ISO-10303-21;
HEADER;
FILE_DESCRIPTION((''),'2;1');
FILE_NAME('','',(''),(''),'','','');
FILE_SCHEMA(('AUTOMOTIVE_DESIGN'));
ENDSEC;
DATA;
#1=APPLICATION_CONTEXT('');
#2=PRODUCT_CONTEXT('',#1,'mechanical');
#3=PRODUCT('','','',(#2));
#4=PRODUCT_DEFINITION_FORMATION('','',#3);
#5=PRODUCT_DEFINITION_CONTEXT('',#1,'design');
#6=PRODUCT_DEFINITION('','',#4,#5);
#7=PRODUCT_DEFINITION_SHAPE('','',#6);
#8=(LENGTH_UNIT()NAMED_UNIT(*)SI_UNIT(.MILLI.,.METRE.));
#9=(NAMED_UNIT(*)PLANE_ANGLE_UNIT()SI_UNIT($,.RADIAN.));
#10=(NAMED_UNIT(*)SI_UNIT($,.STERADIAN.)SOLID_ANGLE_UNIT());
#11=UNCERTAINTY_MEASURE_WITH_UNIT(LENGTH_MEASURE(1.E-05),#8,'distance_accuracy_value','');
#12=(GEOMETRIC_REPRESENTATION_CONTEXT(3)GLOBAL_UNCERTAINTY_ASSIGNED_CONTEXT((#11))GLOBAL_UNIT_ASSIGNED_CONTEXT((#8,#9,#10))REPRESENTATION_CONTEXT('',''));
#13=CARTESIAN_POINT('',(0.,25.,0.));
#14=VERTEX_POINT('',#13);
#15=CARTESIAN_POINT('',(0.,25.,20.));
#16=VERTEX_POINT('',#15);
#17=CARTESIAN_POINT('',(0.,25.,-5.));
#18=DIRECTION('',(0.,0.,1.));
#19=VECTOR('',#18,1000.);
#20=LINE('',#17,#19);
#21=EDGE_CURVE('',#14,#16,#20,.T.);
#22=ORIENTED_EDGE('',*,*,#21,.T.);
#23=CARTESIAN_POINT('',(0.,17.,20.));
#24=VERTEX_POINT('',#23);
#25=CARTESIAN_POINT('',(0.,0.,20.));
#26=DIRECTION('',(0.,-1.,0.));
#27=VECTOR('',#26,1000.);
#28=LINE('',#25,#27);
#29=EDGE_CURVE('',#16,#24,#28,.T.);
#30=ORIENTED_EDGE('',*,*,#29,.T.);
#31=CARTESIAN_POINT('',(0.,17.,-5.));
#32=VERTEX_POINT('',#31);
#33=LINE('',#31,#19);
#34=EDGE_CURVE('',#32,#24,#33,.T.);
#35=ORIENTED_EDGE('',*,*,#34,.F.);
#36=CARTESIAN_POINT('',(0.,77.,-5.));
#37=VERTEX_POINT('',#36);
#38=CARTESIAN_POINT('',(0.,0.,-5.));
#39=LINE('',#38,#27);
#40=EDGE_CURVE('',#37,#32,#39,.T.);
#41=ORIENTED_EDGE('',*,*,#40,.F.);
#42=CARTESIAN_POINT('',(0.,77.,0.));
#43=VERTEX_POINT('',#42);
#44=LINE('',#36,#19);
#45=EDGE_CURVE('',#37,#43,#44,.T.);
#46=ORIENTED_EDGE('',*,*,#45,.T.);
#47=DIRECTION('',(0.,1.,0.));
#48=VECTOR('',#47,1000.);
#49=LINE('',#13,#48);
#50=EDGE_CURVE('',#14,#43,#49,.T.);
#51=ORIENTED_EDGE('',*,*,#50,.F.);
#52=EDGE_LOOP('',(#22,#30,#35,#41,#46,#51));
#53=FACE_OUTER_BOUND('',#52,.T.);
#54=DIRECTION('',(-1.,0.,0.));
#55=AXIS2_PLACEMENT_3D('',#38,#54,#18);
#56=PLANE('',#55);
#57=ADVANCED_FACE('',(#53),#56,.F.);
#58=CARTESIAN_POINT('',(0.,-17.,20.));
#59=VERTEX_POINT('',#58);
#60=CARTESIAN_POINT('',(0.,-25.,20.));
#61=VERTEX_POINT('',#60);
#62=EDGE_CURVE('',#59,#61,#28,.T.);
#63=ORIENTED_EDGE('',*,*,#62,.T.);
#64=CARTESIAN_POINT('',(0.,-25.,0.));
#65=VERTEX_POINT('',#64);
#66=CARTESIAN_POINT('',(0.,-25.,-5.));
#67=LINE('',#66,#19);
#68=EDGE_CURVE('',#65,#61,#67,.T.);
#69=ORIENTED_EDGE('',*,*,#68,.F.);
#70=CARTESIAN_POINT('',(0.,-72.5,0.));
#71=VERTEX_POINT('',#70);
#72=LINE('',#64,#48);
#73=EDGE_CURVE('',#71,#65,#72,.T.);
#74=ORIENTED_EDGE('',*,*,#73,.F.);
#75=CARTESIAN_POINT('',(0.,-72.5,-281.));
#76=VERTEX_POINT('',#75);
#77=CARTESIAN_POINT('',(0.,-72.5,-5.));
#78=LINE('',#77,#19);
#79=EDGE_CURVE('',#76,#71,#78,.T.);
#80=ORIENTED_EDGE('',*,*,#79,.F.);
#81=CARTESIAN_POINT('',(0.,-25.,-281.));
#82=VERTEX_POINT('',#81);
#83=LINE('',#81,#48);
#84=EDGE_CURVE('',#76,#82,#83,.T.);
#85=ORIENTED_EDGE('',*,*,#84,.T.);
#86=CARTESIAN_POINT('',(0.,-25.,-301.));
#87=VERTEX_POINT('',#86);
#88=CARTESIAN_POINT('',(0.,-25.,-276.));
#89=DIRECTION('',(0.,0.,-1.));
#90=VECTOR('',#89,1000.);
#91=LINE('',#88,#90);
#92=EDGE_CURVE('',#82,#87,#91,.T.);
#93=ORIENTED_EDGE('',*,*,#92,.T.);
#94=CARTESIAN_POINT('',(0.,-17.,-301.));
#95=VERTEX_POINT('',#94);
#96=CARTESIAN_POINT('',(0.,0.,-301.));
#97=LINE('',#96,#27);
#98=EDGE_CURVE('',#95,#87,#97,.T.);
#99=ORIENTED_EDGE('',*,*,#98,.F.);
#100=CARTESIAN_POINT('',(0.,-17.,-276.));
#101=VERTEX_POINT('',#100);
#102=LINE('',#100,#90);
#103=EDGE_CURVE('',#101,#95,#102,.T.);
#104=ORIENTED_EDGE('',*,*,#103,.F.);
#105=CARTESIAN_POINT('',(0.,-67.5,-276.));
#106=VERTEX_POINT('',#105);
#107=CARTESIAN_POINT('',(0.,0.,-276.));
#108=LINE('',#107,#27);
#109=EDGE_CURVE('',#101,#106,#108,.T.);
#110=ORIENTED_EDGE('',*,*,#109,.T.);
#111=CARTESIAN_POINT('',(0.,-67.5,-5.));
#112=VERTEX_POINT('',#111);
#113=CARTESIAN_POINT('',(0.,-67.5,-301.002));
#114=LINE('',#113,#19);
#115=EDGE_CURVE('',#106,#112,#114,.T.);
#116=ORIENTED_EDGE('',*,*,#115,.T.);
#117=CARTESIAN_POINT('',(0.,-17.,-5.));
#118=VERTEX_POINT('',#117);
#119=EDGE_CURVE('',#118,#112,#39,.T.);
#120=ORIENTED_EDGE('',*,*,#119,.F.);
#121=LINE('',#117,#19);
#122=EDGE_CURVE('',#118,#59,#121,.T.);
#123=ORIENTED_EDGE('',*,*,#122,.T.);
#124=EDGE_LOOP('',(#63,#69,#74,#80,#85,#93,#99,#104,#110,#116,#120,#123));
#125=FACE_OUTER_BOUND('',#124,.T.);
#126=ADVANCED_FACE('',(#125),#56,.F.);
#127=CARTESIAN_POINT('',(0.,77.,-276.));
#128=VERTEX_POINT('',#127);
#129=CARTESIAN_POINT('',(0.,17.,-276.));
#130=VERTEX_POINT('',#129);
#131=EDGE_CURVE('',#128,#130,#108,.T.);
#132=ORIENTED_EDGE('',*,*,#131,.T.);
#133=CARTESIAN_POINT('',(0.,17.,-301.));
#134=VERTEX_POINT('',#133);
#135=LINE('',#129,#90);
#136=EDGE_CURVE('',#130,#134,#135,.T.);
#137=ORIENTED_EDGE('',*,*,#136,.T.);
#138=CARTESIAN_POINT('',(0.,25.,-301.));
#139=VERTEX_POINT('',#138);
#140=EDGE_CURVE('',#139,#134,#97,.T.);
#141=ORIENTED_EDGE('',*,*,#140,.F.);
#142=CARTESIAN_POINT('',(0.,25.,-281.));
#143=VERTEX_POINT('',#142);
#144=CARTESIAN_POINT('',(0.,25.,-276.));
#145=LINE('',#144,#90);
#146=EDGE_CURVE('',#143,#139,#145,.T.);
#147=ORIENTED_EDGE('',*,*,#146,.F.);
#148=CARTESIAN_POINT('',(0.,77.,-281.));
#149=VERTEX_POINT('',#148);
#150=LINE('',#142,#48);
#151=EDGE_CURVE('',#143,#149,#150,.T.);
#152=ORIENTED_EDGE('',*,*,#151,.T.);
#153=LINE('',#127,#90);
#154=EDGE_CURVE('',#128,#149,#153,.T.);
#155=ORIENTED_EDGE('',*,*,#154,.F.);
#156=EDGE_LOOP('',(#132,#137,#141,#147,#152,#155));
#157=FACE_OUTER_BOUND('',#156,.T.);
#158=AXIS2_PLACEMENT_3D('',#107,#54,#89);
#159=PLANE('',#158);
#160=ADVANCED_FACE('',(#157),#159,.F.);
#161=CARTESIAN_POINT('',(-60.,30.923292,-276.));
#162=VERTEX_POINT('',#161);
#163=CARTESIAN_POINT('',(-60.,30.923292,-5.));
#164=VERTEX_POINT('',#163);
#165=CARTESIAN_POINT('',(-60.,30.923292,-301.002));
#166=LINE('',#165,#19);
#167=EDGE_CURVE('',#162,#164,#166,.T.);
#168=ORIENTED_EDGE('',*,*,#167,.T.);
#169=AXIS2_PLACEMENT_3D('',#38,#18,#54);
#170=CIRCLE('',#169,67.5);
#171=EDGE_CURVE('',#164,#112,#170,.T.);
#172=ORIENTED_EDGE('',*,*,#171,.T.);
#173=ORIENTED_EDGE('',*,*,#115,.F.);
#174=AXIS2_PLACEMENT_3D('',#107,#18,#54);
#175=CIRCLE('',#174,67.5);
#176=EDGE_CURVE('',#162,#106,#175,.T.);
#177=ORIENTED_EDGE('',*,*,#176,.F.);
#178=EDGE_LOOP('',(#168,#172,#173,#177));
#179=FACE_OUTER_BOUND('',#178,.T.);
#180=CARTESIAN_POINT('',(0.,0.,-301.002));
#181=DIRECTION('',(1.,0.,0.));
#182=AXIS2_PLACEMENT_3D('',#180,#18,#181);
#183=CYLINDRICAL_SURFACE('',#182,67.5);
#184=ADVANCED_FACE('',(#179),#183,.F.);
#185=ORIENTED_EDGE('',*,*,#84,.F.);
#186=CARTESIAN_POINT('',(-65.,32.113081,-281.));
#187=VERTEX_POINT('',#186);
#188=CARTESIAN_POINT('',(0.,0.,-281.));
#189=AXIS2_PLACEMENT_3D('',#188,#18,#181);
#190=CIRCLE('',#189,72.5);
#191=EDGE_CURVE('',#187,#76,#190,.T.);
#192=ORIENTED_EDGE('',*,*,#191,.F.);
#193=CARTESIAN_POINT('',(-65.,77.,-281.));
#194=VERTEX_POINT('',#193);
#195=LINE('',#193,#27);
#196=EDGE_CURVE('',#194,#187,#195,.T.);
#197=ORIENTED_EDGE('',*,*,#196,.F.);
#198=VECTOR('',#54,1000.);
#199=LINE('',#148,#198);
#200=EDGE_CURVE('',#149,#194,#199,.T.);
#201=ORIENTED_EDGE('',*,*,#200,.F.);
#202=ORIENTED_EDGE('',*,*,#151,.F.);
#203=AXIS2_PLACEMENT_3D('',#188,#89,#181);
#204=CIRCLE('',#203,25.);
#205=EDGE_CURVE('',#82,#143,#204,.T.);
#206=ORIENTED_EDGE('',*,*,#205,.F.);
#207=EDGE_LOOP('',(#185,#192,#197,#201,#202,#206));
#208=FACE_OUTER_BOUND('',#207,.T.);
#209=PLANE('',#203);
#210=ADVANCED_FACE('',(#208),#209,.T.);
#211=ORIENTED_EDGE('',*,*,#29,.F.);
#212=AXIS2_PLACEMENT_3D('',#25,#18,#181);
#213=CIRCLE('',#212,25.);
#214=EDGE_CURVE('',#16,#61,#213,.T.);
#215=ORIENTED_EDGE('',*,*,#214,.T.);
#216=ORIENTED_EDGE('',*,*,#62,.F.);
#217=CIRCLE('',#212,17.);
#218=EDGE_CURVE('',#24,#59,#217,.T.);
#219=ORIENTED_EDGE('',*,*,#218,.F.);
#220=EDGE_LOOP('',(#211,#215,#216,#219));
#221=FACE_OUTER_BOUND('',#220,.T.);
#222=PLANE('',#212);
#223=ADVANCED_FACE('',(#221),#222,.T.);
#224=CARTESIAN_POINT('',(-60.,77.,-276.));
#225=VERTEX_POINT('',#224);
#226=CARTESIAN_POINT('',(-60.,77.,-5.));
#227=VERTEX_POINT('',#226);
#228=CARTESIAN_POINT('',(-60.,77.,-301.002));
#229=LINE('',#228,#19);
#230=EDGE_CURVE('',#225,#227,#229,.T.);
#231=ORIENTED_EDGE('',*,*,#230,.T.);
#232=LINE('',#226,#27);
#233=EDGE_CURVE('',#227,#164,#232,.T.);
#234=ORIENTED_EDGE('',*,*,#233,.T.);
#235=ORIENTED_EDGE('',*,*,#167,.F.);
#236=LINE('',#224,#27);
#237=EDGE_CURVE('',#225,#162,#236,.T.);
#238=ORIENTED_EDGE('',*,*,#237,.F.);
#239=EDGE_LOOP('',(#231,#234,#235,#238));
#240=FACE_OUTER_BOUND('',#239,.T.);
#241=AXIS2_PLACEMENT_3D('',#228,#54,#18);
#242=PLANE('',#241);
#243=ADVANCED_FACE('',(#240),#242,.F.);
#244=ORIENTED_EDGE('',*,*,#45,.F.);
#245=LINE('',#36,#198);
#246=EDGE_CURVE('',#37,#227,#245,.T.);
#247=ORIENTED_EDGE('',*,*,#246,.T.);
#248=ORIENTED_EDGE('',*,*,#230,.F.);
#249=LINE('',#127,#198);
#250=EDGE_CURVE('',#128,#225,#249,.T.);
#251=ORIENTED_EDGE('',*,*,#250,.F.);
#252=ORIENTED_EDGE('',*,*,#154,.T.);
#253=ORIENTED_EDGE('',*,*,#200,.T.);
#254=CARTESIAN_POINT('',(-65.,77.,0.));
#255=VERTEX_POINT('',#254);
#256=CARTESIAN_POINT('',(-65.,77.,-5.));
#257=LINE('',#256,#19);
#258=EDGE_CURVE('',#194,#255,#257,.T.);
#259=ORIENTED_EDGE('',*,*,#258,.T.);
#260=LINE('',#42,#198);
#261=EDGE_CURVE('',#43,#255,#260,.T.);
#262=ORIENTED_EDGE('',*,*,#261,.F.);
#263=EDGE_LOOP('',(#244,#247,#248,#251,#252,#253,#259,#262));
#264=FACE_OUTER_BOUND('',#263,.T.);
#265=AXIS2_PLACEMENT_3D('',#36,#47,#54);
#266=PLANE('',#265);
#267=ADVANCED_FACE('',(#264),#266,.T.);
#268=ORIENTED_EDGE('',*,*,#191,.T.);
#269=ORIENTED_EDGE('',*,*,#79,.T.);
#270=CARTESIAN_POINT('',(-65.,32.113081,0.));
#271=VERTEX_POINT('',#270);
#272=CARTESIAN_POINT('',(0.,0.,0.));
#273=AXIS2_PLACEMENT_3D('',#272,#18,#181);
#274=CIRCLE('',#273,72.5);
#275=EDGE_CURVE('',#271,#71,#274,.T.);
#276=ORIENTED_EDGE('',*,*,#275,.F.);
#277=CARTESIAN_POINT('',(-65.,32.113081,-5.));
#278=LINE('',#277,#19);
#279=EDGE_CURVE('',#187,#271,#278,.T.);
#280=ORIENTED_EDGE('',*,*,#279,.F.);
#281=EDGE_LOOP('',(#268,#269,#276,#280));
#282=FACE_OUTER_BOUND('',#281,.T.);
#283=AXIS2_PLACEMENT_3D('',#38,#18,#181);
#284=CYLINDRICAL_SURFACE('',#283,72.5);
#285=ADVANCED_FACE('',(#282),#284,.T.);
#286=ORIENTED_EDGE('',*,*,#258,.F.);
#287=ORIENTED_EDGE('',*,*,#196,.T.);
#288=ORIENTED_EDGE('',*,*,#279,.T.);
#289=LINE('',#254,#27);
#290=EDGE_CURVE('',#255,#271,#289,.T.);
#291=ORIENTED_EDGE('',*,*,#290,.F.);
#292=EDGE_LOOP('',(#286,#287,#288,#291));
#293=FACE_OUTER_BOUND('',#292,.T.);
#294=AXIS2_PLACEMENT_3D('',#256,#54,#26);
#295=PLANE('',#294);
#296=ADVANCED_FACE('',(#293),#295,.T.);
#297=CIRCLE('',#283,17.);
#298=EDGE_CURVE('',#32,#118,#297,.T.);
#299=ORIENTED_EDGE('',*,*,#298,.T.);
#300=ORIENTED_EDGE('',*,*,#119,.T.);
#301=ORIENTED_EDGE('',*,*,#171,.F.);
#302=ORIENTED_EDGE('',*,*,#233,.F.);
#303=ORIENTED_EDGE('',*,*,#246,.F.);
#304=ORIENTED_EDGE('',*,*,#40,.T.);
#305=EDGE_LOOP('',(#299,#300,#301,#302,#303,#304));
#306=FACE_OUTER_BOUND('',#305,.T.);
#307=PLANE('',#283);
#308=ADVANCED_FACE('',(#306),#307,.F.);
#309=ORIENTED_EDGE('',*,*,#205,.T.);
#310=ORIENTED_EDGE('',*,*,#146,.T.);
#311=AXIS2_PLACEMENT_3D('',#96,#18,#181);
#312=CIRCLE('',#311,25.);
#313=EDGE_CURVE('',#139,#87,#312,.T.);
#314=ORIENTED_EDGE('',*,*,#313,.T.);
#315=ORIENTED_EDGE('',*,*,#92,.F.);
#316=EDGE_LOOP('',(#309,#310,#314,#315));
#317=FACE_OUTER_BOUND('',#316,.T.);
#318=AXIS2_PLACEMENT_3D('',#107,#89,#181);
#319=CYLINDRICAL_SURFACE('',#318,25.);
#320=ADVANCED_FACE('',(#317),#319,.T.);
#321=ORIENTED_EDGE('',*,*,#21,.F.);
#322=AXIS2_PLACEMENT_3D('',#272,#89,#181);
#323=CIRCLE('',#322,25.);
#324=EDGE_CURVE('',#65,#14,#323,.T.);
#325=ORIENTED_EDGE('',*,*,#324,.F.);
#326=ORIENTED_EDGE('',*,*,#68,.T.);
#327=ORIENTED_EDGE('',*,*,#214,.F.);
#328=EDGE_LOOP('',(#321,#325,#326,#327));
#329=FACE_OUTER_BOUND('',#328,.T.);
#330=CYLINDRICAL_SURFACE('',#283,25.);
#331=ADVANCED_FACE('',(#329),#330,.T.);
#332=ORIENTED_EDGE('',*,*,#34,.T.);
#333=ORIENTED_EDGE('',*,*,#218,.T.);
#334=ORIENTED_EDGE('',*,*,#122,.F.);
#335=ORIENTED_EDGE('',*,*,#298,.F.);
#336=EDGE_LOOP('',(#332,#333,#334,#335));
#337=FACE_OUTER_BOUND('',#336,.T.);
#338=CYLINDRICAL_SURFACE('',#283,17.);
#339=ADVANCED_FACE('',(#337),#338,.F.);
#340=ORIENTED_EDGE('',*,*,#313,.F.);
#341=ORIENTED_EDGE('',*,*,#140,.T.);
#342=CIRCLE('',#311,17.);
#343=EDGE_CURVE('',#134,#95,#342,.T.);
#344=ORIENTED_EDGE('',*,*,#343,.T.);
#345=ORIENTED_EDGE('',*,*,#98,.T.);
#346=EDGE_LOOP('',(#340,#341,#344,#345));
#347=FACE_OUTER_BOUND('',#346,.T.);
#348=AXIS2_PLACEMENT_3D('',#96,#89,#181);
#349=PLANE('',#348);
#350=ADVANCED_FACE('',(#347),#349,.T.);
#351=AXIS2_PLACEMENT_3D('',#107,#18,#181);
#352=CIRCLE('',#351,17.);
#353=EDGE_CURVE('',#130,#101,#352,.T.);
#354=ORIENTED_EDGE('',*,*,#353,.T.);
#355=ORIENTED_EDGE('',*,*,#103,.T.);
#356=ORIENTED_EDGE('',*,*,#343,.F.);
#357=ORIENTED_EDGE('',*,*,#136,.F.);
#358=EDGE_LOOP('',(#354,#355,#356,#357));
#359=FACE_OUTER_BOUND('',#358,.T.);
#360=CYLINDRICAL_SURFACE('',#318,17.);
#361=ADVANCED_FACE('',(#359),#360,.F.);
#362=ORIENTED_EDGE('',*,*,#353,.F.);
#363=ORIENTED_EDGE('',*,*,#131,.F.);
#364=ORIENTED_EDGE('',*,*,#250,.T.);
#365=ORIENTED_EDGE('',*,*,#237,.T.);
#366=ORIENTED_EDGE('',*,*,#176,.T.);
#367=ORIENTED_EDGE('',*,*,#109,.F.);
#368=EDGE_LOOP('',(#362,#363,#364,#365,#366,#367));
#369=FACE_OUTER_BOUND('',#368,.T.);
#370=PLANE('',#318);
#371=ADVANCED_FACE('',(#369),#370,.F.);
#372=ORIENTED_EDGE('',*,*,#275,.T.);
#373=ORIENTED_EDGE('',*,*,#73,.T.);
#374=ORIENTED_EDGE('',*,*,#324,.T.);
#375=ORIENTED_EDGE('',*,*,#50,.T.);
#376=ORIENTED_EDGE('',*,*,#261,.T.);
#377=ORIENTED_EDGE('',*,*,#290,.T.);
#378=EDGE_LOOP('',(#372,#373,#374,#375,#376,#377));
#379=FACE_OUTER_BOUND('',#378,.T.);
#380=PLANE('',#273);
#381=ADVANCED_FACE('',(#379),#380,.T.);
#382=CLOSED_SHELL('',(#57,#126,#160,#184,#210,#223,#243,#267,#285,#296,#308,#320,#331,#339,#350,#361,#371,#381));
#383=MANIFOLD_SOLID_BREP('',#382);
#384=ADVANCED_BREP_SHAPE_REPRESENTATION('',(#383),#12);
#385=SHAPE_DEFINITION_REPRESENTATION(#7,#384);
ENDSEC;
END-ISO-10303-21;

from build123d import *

# Parameters (mm, degrees)
TROUGH_SHELL_DEPTH      = 20
TROUGH_SHELL_DEPTH_BACK = 5
END_START               = -5
END_PLATE_DEPTH         = 5
SIDE_WALLS_REACH        = 316.327


with BuildPart() as part:
    # Trough Profile Sketch → Trough Shell (new, two sides: drawn at the far end of the back side and taken through both)
    with BuildSketch(Plane.XY.offset(-TROUGH_SHELL_DEPTH_BACK)):
        with BuildLine():
            Line((0, 17), (0, 25))
            ThreePointArc((0, 25), (-25, 0), (0, -25))
            Line((0, -25), (0, -17))
            ThreePointArc((0, -17), (-17, 0), (0, 17))
        make_face()
    extrude(amount=TROUGH_SHELL_DEPTH + TROUGH_SHELL_DEPTH_BACK)

    # End Plate Sketch → End Plate (add)
    with BuildSketch(Plane.XY.offset(END_START)):
        with BuildLine():
            Line((0, 25), (0, 77))
            Line((0, 77), (-65, 77))
            Line((-65, 77), (-65, 32.113081447))
            ThreePointArc((-65, 32.113081447), (-61.581037686, -38.262590053), (0, -72.5))
            Line((0, -72.5), (0, -25))
            ThreePointArc((0, -25), (-25, 0), (0, 25))
        make_face()
    extrude(amount=END_PLATE_DEPTH)


with BuildPart() as body_2:
    # End Plate Mirror: mirrored copy
    add(part.part.mirror(Plane.XY.offset(-140.5)))

    # Side Wall Sketch → Side Walls (add, up to next)
    with BuildSketch(Plane(origin=(0, 0, -5), x_dir=(-1, 0, 0), z_dir=(0, 0, -1)), mode=Mode.PRIVATE) as side_walls_sk1:
        with BuildLine():
            Line((65, 77), (65, 32.113081447))
            ThreePointArc((65, 32.113081447), (61.581037686, -38.262590053), (0, -72.5))
            Line((0, -72.5), (0, -67.5))
            ThreePointArc((0, -67.5), (57.634938288, -35.134938288), (60, 30.923292192))
            Line((60, 30.923292192), (60, 77))
            Line((60, 77), (65, 77))
        make_face()
    side_walls_tool1 = extrude(side_walls_sk1.sketch, amount=SIDE_WALLS_REACH, mode=Mode.PRIVATE) - body_2.part

    add(part.part)  # Side Walls merges part
    add(side_walls_tool1.solids().sort_by_distance((-61.66152, 53.961646, -5))[0])


solid = body_2.part
